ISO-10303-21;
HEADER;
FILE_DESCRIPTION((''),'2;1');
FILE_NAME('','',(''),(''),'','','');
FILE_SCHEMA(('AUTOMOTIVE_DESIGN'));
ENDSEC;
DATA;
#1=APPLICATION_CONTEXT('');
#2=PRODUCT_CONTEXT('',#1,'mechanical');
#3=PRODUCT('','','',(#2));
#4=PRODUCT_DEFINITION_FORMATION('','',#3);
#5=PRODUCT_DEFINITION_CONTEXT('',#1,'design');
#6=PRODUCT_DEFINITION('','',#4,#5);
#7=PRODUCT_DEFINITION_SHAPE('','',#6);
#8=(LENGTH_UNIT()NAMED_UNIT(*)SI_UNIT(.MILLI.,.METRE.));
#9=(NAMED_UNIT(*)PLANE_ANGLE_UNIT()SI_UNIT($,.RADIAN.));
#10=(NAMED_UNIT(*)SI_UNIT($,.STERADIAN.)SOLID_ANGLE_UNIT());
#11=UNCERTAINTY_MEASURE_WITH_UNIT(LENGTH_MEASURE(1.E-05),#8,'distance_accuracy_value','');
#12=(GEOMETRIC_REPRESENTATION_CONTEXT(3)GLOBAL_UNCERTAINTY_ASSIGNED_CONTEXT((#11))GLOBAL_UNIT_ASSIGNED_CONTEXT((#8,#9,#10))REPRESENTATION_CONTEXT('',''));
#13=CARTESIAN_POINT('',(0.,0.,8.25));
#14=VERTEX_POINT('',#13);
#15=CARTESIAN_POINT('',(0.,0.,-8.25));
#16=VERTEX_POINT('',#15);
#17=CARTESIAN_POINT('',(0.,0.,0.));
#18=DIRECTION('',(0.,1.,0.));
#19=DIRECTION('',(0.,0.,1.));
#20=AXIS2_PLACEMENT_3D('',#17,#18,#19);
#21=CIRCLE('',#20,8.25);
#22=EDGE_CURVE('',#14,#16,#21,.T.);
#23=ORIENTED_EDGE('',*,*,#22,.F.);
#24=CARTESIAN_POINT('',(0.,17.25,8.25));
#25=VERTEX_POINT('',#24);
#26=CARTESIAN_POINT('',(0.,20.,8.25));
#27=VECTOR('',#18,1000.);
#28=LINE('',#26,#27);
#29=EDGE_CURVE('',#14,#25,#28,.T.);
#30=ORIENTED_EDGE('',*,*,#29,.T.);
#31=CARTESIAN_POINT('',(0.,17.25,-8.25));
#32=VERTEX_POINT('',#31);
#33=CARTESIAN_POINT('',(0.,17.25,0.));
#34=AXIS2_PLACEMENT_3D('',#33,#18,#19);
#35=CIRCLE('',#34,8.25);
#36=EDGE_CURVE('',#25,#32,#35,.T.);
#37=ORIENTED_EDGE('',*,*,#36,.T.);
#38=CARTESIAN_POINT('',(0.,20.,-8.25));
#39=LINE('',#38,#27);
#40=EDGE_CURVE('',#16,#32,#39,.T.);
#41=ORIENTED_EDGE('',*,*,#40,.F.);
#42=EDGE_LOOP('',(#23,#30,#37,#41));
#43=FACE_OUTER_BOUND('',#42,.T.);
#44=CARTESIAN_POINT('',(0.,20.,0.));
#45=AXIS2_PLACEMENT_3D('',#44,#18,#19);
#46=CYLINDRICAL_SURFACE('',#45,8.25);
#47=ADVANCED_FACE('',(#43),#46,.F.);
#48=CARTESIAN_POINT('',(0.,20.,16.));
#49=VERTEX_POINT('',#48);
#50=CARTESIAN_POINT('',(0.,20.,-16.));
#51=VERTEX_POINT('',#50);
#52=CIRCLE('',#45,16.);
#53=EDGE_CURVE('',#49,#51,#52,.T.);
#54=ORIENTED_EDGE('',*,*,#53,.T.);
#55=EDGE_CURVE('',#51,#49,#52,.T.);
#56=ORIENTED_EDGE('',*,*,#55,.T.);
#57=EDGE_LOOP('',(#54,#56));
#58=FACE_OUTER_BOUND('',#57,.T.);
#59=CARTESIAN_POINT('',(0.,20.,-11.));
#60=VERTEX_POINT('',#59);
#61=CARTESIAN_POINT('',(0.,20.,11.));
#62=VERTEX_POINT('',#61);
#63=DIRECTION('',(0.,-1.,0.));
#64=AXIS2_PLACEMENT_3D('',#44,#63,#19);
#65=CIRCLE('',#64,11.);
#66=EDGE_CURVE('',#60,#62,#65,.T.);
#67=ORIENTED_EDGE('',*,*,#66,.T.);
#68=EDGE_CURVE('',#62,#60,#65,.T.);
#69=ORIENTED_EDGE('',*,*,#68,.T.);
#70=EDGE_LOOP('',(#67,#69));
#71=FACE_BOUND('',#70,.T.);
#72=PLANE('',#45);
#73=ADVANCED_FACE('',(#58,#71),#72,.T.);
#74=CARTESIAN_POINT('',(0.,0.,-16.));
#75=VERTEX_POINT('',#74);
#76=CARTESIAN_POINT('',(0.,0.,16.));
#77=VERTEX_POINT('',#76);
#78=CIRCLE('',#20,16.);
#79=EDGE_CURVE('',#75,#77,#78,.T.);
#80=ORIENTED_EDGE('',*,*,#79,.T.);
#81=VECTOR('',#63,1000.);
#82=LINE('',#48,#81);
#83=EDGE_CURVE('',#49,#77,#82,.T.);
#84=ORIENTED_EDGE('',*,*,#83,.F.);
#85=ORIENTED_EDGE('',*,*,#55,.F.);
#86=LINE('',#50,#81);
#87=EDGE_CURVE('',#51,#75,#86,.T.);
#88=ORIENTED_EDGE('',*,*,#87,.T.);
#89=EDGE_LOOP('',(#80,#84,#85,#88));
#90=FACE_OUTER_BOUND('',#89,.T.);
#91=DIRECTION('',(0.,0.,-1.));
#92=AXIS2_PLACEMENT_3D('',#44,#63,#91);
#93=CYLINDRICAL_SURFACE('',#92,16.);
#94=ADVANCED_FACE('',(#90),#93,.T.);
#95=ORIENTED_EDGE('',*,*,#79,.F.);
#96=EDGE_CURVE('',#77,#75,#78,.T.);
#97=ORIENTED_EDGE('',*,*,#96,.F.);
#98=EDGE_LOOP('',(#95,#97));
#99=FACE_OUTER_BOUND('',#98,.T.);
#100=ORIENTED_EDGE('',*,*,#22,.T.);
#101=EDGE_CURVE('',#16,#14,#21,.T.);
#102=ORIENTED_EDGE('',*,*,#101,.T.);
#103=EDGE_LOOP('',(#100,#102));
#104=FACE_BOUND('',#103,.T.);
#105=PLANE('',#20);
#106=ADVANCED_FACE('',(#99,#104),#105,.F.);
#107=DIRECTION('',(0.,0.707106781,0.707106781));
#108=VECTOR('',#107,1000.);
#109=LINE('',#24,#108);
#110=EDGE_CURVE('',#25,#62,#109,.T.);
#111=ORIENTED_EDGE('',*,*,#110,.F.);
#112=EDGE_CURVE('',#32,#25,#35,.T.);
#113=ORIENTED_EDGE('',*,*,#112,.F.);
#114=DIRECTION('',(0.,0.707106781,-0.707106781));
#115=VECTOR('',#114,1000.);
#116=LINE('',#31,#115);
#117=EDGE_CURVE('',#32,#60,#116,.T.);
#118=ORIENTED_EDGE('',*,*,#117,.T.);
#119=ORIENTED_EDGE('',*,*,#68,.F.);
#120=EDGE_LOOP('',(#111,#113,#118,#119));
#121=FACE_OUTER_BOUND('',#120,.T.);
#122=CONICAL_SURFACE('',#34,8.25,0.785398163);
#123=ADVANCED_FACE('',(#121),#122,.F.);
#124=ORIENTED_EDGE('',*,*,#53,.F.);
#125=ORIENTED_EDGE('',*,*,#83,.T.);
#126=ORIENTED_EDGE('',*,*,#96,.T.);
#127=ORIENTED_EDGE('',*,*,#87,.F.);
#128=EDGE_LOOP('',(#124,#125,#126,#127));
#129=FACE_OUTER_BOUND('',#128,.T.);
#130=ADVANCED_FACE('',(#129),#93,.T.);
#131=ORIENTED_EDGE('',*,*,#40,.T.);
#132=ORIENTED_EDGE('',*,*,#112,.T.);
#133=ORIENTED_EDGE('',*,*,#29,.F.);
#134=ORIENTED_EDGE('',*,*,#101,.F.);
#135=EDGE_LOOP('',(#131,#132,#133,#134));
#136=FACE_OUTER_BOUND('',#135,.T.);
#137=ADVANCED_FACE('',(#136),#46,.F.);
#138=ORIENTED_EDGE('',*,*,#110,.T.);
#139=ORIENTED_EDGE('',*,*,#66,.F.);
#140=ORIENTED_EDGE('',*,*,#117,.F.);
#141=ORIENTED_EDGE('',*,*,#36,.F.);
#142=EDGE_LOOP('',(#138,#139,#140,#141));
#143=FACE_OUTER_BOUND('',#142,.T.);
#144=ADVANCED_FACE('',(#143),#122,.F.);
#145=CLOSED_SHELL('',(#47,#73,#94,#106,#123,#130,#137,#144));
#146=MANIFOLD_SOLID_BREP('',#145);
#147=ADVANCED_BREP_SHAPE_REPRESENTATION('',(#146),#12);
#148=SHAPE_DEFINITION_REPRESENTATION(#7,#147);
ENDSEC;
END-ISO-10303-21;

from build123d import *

# Parameters (mm, degrees)
SKETCH1_R                  = 16
SKETCH1_R_2                = 7.5
BOSS_EXTRUDE1_DEPTH        = 20
M18X1_5_TAPPED_HOLE2_D     = 16.5
M18X1_5_TAPPED_HOLE2_DEPTH = 30
M18X1_5_TAPPED_HOLE2_TIP   = 4.957100107
CHAMFER1_SIZE              = 2.75


with BuildPart() as part:
    # Sketch1 → Boss-Extrude1 (new body)
    with BuildSketch(Plane(origin=(0, 0, 0), x_dir=(1, 0, 0), z_dir=(0, 1, 0))):
        with Locations(Location((0, 0, 0), (0, 0, 270))):
            Circle(SKETCH1_R)
        with Locations(Location((0, 0, 0), (0, 0, 270))):
            Circle(SKETCH1_R_2, mode=Mode.SUBTRACT)
    extrude(amount=BOSS_EXTRUDE1_DEPTH)

    # M18x1.5 Tapped Hole2
    with Locations(Plane(origin=(0, 20, 0), x_dir=(1, 0, 0), z_dir=(0, 1, 0))):
        with Locations((0, 0)):
            Hole(M18X1_5_TAPPED_HOLE2_D / 2, depth=M18X1_5_TAPPED_HOLE2_DEPTH)
            with Locations((0, 0, -(M18X1_5_TAPPED_HOLE2_DEPTH + M18X1_5_TAPPED_HOLE2_TIP / 2))):  # 118° drill point
                Cone(0, M18X1_5_TAPPED_HOLE2_D / 2, M18X1_5_TAPPED_HOLE2_TIP, mode=Mode.SUBTRACT)

    # Chamfer1
    chamfer1_edges = [part.edges().sort_by_distance(p)[0] for p in [
        (8.25, 20, 0),
    ]]
    chamfer(chamfer1_edges, length=CHAMFER1_SIZE)


solid = part.part
